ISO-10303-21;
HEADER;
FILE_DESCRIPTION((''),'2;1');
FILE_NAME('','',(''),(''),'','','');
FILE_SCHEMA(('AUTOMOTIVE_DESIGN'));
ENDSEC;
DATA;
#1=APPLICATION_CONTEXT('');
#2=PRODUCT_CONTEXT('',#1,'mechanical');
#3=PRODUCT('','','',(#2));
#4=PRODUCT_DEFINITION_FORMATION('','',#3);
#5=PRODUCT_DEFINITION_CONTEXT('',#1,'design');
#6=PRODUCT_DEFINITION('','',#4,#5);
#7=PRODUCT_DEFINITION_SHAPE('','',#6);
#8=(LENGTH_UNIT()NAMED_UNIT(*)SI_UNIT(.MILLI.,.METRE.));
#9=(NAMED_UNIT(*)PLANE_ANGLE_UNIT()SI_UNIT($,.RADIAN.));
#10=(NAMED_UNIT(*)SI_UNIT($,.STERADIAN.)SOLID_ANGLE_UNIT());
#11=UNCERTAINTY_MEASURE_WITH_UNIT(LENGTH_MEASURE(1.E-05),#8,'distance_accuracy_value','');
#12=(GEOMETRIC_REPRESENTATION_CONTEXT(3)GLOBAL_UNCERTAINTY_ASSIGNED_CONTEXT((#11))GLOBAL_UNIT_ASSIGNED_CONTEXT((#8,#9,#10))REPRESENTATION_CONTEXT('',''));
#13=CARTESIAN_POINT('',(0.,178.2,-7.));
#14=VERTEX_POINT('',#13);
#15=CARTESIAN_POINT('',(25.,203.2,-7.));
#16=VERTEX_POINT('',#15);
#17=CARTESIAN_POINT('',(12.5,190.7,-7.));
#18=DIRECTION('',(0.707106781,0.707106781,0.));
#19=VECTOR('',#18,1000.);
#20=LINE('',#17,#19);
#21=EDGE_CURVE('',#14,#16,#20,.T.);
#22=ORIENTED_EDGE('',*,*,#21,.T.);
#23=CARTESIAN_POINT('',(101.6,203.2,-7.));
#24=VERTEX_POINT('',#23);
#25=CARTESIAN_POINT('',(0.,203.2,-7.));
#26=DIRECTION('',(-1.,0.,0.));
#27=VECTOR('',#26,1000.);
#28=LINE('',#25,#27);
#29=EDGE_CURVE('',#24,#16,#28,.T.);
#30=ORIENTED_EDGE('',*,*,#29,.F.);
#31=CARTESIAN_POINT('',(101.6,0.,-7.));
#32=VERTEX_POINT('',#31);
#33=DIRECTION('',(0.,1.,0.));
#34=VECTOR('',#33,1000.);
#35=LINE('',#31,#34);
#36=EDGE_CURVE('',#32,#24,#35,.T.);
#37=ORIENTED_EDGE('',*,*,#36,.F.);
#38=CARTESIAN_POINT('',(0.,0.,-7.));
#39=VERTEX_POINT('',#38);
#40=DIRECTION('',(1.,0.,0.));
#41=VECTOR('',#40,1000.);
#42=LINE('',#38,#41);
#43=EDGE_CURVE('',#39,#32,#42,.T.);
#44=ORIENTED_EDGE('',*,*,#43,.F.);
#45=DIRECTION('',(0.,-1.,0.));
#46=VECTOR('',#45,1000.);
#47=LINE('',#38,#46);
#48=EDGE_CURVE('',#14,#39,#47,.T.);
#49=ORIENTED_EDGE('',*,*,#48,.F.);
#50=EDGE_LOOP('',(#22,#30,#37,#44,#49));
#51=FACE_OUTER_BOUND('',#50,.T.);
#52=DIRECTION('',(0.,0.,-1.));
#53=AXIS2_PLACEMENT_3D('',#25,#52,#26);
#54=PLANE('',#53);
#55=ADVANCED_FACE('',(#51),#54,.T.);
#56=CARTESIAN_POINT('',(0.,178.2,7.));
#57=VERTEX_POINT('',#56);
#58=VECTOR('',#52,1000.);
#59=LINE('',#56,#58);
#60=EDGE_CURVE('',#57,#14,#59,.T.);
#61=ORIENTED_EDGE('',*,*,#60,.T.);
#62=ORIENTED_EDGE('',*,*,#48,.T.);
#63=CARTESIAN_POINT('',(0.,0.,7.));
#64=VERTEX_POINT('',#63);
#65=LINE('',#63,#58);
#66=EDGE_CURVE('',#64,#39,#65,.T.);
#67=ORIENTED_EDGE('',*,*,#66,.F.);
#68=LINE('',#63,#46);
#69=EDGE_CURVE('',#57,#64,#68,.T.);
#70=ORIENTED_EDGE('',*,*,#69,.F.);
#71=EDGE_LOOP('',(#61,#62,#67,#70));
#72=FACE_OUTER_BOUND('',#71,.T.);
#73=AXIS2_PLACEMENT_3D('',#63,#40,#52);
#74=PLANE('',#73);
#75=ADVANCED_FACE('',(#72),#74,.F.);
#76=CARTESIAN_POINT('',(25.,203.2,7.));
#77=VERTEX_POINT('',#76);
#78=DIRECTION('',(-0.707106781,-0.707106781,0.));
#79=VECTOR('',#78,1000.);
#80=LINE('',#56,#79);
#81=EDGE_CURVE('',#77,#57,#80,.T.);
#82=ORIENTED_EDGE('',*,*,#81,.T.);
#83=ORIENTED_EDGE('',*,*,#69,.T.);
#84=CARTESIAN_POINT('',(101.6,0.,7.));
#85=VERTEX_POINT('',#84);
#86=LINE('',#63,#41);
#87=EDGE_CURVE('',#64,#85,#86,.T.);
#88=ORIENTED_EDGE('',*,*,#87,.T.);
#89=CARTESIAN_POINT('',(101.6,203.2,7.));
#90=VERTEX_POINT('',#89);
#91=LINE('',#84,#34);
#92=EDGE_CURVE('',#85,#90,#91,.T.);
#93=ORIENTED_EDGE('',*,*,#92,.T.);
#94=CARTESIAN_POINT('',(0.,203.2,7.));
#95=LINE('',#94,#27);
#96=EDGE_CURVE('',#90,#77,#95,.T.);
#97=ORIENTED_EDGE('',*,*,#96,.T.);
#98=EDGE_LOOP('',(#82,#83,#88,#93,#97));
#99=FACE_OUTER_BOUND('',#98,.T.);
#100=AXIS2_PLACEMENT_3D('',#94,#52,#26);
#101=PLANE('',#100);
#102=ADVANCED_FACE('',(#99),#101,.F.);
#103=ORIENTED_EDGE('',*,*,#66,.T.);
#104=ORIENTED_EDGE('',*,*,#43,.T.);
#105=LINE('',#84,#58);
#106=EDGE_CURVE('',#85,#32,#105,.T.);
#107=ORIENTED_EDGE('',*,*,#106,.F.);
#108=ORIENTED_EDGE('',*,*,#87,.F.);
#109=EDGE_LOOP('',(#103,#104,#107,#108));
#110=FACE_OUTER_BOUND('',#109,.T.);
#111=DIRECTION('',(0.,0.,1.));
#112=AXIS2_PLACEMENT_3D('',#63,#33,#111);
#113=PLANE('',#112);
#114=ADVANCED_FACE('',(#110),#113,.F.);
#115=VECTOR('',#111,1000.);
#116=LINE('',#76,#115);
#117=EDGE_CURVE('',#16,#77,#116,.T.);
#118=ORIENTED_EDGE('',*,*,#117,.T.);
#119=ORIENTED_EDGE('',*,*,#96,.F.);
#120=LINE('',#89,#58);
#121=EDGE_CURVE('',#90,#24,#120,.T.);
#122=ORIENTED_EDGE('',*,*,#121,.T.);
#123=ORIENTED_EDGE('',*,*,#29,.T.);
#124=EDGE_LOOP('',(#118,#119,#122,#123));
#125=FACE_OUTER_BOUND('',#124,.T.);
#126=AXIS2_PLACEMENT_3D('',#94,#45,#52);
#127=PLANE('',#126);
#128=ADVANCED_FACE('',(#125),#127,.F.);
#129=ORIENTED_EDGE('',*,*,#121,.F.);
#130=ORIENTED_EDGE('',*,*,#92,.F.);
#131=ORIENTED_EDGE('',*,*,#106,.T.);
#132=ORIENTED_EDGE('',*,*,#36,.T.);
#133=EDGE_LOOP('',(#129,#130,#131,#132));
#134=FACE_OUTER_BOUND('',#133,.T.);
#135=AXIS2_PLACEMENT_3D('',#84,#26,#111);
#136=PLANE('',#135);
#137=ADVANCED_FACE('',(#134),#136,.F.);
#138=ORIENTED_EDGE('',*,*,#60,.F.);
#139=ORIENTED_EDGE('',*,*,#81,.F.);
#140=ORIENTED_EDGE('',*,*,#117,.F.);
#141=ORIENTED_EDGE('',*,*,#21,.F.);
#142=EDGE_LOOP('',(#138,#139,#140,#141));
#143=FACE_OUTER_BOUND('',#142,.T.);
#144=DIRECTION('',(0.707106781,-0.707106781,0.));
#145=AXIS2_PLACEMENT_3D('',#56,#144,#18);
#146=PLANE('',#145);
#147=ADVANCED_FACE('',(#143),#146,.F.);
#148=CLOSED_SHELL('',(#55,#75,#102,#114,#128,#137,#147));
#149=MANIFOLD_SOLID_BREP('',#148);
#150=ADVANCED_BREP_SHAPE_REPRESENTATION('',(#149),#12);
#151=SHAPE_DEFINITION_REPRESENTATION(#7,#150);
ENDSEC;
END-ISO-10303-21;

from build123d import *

# Parameters (mm, degrees)
SKETCH1_W      = 101.6
SKETCH1_H      = 203.2
EXTRUDE1_DEPTH = 7
CHAMFER1_SIZE  = 25


with BuildPart() as part:
    # Sketch1 → Extrude1 (new, symmetric)
    with BuildSketch(Plane.XY):
        with Locations((50.8, 101.6)):
            Rectangle(SKETCH1_W, SKETCH1_H)
    extrude(amount=EXTRUDE1_DEPTH, both=True)

    # Chamfer1
    chamfer1_edges = [part.edges().sort_by_distance(p)[0] for p in [
        (0, 203.2, 0),
    ]]
    chamfer(chamfer1_edges, length=CHAMFER1_SIZE)


solid = part.part
